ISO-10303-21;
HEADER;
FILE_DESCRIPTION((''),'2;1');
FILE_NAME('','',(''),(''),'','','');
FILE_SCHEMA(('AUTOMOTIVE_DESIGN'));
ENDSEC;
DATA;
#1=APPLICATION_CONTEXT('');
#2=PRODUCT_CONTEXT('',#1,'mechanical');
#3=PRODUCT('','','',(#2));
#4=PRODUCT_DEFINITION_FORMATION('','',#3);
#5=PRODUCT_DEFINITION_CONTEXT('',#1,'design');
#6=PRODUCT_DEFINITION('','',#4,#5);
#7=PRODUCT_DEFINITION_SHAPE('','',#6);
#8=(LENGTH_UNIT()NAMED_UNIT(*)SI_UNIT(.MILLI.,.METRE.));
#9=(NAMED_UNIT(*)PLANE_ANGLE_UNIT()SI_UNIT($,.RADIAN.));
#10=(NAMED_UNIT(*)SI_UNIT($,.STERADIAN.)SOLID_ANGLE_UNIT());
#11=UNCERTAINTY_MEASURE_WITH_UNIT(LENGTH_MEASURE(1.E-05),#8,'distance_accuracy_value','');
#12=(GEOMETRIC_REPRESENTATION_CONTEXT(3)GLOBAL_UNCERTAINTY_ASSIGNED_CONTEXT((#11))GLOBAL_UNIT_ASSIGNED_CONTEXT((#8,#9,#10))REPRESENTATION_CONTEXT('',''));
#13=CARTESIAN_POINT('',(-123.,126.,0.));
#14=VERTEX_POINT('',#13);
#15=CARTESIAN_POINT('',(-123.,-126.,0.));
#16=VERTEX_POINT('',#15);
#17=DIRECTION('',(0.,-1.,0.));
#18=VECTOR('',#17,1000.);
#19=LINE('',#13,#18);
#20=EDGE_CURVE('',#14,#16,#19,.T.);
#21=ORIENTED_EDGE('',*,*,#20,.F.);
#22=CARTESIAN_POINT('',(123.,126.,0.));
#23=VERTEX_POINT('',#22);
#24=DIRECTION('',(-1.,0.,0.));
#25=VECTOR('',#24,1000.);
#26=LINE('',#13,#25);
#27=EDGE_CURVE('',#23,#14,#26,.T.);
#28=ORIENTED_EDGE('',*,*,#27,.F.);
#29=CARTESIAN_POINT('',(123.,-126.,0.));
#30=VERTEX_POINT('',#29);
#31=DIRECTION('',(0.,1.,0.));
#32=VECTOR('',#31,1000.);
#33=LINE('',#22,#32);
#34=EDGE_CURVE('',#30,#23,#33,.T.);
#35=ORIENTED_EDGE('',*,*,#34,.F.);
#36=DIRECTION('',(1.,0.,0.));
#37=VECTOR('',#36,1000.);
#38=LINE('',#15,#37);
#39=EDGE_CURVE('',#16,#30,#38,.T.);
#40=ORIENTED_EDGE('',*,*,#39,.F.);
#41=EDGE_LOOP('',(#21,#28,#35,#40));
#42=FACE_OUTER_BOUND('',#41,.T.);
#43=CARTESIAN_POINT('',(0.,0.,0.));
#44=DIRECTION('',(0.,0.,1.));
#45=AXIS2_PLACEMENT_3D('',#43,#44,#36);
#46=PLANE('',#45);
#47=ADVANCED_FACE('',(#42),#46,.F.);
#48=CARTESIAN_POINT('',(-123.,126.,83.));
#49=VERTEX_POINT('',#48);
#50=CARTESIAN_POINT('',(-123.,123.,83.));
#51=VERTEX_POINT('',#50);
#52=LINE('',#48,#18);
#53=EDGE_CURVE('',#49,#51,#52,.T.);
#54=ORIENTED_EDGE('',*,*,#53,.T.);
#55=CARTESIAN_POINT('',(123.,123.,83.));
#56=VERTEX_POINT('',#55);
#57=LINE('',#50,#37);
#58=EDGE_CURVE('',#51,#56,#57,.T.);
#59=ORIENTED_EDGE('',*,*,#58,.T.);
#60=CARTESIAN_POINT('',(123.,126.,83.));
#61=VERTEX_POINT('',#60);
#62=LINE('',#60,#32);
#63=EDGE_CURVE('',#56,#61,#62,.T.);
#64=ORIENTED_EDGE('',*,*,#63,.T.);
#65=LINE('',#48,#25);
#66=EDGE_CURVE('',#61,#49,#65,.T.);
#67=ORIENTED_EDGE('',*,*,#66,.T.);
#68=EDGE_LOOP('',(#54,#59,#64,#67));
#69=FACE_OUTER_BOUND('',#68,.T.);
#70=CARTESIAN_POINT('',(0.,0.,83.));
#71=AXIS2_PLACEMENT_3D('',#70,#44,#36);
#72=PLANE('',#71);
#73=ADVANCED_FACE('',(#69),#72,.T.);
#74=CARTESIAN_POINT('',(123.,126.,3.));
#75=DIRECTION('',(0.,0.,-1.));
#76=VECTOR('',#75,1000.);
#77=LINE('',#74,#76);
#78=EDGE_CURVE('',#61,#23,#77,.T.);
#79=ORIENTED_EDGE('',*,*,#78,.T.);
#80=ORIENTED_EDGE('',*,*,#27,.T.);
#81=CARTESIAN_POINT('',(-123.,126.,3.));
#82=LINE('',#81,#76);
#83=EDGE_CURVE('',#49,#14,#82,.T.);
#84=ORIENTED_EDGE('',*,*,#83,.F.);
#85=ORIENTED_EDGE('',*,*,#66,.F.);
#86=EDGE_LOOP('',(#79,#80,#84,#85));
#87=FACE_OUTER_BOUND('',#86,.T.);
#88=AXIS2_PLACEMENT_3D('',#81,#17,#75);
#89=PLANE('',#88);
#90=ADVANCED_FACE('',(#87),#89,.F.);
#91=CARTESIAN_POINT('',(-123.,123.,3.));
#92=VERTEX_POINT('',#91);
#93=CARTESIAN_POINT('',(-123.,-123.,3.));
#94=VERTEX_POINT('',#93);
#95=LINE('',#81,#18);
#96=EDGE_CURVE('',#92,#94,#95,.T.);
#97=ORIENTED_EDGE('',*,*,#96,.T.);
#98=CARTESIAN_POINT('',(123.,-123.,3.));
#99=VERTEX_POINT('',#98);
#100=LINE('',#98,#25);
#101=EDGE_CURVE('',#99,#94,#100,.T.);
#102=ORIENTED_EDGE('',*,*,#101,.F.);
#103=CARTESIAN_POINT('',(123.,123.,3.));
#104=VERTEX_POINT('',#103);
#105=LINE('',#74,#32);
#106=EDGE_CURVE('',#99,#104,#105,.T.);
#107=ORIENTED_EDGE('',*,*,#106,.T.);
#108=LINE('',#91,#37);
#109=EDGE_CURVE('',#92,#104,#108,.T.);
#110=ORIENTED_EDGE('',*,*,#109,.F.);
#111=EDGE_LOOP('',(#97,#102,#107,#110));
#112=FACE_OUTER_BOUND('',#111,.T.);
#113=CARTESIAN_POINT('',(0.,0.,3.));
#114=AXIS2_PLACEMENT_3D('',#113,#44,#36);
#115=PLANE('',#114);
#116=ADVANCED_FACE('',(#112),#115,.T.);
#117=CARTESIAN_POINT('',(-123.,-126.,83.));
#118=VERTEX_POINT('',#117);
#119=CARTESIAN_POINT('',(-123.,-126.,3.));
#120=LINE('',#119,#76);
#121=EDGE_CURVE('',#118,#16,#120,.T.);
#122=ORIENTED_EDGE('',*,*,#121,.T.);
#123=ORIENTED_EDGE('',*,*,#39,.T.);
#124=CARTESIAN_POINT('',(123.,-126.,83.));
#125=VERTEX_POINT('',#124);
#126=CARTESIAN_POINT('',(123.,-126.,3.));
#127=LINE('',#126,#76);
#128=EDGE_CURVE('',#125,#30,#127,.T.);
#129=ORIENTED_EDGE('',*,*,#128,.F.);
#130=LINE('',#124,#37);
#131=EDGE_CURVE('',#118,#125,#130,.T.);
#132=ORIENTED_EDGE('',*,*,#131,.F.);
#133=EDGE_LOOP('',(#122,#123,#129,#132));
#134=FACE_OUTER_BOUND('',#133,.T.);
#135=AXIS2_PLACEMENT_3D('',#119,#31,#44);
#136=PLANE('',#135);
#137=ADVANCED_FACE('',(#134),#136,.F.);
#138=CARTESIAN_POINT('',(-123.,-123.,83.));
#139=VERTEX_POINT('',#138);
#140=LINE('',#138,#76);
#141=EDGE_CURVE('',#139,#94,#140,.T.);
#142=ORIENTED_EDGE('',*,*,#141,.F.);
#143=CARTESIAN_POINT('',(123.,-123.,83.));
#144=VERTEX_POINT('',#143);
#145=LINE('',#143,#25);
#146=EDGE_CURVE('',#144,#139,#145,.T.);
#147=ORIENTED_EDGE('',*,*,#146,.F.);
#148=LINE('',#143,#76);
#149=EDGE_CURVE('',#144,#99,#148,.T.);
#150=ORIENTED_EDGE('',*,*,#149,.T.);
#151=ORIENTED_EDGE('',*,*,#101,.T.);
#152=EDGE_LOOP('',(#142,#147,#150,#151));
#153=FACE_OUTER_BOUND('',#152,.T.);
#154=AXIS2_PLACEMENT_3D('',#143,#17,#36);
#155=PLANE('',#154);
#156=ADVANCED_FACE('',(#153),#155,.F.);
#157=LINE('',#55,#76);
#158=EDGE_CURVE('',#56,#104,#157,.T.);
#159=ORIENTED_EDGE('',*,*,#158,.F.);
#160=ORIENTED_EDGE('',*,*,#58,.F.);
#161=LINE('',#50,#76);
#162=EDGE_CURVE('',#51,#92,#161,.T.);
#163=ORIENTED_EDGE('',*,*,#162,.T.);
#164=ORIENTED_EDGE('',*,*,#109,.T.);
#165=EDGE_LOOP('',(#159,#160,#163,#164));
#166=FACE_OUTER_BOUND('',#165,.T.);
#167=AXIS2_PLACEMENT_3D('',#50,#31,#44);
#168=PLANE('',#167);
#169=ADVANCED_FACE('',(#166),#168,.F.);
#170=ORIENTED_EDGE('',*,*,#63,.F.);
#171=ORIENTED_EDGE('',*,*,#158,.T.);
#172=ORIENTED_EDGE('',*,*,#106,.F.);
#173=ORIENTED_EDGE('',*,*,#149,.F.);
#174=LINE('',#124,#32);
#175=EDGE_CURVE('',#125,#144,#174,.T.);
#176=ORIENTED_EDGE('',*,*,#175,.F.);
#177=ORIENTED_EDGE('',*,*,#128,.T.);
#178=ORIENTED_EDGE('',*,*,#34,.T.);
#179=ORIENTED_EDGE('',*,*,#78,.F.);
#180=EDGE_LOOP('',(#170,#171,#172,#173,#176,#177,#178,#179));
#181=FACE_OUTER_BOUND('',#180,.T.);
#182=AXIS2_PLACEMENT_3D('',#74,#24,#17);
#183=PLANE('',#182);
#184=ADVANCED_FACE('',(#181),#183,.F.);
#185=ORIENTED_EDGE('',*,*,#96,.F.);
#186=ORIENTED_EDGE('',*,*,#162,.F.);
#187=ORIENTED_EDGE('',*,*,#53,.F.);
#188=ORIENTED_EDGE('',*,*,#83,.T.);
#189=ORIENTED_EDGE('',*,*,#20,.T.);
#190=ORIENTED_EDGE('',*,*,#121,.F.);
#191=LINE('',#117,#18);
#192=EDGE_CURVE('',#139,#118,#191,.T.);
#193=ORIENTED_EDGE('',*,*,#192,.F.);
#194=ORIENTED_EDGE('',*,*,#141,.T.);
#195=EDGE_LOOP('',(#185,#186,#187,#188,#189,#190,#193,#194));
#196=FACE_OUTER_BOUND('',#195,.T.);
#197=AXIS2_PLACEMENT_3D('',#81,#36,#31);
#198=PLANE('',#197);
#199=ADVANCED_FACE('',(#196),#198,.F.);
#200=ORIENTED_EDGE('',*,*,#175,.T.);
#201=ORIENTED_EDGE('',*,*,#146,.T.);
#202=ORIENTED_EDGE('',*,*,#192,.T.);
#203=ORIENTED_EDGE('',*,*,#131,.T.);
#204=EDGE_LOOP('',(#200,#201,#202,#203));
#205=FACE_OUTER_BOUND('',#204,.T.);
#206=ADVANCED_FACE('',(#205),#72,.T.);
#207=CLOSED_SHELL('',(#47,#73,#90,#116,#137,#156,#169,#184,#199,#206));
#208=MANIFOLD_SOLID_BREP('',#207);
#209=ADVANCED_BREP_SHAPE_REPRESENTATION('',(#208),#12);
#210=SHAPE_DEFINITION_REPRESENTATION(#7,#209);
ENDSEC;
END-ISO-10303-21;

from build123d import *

# Parameters (mm, degrees)
SKETCH1_W           = 246
SKETCH1_H           = 252
BOSS_EXTRUDE1_DEPTH = 3
SKETCH2_W           = 246
SKETCH2_H           = 3
BOSS_EXTRUDE2_DEPTH = 80


with BuildPart() as part:
    # Sketch1 → Boss-Extrude1 (new body)
    with BuildSketch(Plane.XY):
        Rectangle(SKETCH1_W, SKETCH1_H)
    extrude(amount=BOSS_EXTRUDE1_DEPTH)

    # Sketch2 → Boss-Extrude2 (add)
    with BuildSketch(Plane.XY.offset(3)):
        with Locations((0, 124.5)):
            Rectangle(SKETCH2_W, SKETCH2_H)
        with Locations((0, -124.5)):
            Rectangle(SKETCH2_W, SKETCH2_H)
    extrude(amount=BOSS_EXTRUDE2_DEPTH)


solid = part.part
